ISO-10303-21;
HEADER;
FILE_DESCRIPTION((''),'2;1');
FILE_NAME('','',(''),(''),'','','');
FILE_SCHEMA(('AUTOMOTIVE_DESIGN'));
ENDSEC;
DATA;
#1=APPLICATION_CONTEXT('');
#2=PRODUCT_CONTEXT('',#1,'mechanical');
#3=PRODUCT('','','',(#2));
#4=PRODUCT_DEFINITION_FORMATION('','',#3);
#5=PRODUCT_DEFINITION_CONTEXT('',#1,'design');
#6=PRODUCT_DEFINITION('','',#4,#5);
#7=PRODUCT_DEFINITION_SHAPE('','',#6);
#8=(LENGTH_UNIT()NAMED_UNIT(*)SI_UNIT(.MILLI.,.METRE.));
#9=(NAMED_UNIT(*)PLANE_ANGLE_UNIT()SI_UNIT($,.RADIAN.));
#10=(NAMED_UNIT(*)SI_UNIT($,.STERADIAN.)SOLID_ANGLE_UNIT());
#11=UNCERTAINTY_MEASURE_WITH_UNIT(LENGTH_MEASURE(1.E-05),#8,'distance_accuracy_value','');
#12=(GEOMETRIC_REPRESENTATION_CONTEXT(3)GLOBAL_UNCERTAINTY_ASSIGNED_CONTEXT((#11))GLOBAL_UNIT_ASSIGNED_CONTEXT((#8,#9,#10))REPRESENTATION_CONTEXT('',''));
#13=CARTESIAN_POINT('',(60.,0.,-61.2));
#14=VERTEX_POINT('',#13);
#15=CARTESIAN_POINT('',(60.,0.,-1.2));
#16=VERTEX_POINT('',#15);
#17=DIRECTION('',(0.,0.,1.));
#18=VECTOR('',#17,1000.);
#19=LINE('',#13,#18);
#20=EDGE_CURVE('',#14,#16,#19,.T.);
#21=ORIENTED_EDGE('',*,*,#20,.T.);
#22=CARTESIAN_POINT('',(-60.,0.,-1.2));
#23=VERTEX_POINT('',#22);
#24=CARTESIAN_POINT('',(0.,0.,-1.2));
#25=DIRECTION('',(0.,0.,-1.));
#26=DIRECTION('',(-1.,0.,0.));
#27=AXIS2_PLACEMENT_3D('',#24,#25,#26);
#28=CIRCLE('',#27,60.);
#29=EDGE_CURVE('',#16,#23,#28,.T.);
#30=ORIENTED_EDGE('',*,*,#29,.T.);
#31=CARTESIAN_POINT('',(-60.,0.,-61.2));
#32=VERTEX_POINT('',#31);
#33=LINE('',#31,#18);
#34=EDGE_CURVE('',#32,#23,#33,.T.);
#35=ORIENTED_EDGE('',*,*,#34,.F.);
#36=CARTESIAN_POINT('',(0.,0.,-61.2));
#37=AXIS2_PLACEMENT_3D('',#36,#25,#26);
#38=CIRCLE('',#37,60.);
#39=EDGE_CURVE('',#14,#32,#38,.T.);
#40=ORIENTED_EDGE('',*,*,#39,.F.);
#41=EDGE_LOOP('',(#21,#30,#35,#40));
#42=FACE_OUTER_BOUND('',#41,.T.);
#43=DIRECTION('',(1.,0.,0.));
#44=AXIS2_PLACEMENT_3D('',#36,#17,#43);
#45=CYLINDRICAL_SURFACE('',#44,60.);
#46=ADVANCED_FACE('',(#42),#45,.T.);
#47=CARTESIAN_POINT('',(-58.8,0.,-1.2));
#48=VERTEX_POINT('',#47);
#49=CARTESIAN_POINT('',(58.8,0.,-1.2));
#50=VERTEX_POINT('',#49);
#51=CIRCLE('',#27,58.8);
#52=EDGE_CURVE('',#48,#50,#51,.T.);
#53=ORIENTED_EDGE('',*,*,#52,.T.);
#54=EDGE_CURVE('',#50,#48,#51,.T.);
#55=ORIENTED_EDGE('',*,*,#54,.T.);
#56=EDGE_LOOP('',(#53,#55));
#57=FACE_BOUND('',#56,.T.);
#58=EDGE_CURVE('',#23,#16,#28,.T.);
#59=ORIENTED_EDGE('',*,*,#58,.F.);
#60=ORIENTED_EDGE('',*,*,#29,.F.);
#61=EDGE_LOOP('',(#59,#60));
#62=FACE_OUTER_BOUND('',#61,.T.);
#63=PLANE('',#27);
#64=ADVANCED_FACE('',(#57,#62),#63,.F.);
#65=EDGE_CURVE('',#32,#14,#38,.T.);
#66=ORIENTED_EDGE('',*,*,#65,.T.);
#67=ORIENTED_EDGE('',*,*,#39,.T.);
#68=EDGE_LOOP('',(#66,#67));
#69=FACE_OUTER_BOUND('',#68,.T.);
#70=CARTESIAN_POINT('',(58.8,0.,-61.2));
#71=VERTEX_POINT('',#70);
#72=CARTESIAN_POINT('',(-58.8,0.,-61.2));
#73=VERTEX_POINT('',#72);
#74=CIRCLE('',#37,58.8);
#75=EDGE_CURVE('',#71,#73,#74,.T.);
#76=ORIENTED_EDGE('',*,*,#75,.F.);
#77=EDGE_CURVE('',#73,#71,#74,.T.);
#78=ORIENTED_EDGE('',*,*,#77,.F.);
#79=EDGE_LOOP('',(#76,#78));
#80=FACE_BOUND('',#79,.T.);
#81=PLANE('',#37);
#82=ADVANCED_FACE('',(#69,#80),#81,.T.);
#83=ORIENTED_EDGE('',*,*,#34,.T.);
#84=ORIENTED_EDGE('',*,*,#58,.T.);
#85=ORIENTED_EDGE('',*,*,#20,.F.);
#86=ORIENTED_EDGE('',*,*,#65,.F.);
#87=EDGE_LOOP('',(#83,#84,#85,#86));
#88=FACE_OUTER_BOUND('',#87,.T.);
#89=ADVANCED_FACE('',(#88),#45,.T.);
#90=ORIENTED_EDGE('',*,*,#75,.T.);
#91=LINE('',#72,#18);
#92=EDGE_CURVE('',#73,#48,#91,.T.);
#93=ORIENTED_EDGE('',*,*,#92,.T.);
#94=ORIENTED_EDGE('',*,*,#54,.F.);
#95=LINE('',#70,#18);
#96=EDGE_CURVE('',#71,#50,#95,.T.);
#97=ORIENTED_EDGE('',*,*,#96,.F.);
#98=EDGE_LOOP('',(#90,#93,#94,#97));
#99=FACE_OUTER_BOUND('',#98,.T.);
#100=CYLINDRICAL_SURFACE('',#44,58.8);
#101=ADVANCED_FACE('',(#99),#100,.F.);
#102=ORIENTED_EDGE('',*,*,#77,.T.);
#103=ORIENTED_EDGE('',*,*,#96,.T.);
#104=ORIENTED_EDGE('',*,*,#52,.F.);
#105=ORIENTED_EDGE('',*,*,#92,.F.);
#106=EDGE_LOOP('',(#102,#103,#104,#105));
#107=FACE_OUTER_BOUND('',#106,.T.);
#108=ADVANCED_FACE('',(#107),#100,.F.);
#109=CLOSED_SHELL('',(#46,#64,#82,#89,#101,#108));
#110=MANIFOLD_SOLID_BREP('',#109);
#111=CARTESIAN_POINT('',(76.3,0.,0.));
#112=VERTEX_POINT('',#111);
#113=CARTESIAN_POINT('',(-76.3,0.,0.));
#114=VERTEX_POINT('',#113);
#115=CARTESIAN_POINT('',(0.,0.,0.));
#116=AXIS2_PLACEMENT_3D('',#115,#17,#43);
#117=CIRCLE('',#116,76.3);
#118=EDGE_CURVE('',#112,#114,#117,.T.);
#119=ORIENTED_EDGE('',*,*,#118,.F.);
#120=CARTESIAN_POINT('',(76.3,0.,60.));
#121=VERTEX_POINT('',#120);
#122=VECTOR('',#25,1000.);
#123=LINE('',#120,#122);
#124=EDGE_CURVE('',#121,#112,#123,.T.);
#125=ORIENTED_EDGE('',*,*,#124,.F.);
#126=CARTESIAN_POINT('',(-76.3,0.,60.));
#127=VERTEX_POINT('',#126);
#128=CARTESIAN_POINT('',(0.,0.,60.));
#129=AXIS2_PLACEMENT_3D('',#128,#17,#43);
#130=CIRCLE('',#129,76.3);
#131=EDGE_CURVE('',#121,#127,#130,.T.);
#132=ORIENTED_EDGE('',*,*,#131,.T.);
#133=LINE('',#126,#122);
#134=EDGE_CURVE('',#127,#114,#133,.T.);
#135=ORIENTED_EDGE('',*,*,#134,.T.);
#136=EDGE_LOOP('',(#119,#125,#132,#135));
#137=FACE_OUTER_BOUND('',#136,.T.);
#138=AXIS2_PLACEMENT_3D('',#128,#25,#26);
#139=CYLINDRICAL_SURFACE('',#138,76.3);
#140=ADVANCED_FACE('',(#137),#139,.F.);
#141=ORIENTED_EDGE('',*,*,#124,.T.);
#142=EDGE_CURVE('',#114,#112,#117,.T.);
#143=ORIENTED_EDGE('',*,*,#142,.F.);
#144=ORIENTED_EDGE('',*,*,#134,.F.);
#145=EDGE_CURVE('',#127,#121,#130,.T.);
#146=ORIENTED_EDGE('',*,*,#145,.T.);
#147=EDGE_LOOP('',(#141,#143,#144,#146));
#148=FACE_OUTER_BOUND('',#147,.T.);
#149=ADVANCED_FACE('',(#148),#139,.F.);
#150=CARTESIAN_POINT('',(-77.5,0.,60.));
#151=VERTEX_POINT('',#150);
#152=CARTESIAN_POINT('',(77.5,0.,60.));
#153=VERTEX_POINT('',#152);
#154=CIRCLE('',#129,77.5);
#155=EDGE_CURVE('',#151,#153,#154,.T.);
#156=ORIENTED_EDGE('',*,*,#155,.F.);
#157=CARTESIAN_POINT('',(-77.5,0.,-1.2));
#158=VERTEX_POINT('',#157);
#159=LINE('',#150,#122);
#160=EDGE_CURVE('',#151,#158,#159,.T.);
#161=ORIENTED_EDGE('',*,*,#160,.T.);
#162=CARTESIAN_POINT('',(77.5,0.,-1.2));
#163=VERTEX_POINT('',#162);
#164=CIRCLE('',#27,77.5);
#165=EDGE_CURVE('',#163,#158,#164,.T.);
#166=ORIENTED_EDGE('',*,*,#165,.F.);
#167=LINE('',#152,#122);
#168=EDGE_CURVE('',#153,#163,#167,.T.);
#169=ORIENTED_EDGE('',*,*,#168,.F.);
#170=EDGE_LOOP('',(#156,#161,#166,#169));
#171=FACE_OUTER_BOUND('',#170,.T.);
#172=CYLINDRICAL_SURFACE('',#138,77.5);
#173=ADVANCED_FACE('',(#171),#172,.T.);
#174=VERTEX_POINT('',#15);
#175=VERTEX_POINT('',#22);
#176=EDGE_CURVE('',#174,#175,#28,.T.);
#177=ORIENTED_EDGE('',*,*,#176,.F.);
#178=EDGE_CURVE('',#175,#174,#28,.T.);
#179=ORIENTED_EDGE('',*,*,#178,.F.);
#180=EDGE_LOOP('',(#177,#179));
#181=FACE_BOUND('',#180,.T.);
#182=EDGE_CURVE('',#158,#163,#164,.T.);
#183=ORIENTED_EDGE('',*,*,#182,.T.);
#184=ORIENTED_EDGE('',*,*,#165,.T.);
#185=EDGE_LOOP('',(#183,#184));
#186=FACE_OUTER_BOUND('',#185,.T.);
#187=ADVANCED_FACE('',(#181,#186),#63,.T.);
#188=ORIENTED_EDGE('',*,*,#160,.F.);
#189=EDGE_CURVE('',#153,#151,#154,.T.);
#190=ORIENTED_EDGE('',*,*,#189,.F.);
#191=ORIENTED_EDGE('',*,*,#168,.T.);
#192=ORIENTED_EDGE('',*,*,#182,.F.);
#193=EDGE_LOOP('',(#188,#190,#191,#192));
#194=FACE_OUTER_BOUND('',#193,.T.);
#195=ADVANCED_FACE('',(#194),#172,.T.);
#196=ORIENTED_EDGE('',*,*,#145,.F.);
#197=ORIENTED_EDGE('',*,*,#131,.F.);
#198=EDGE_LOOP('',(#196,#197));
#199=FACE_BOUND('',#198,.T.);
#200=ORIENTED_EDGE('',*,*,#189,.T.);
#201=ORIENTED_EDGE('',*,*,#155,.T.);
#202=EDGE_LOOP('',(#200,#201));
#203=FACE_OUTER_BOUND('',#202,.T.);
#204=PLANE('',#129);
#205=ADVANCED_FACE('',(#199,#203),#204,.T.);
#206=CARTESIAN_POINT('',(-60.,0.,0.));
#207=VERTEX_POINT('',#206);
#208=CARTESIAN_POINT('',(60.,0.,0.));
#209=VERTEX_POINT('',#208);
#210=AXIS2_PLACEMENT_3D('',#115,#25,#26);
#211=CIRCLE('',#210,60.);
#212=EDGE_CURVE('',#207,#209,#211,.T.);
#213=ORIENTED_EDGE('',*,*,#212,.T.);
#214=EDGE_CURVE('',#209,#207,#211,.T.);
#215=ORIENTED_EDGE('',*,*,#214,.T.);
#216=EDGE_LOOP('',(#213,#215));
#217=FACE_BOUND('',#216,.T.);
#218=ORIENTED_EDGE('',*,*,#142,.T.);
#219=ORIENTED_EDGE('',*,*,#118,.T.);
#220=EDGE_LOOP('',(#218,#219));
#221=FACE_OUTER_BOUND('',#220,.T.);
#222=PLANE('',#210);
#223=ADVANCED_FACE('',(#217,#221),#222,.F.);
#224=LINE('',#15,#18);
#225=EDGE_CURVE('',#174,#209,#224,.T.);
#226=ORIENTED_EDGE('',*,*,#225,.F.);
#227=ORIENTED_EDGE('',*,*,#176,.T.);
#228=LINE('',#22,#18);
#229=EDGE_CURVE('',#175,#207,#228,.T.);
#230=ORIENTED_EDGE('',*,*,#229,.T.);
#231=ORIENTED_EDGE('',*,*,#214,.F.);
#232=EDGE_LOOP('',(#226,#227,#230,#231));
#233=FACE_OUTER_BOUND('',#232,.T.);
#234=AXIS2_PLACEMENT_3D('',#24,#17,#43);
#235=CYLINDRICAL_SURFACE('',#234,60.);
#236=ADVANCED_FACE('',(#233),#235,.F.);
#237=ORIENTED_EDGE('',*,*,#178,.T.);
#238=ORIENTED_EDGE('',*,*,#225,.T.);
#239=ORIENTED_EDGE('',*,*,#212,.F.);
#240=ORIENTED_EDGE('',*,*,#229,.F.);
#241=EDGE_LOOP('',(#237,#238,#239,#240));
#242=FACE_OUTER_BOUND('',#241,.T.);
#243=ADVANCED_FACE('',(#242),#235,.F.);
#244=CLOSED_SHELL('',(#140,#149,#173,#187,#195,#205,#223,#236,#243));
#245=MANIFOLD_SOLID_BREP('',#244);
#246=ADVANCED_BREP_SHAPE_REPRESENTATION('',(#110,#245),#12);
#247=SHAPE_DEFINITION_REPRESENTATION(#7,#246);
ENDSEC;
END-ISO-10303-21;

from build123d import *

# Parameters (mm, degrees)
SKETCH1_R           = 77.5
SKETCH1_R_2         = 76.3
BOSS_EXTRUDE1_DEPTH = 60
BOSS_EXTRUDE2_START = 1.2
SKETCH2_R           = 77.5
SKETCH2_R_2         = 60
BOSS_EXTRUDE2_DEPTH = 1.2
SKETCH3_R           = 60
SKETCH3_R_2         = 58.8
BOSS_EXTRUDE3_DEPTH = 60


with BuildPart() as part:
    # Sketch1 → Boss-Extrude1 (new body)
    with BuildSketch(Plane.XY):
        Circle(SKETCH1_R)
        Circle(SKETCH1_R_2, mode=Mode.SUBTRACT)
    extrude(amount=BOSS_EXTRUDE1_DEPTH)

    # Sketch2 → Boss-Extrude2 (add)
    with BuildSketch(Plane(origin=(0, 0, 0), x_dir=(-1, 0, 0), z_dir=(0, 0, -1)).offset(BOSS_EXTRUDE2_START)):
        Circle(SKETCH2_R)
        Circle(SKETCH2_R_2, mode=Mode.SUBTRACT)
    extrude(amount=-BOSS_EXTRUDE2_DEPTH)


with BuildPart() as body_2:
    # Sketch3 → Boss-Extrude3 (new body)
    with BuildSketch(Plane(origin=(0, 0, -1.2), x_dir=(-1, 0, 0), z_dir=(0, 0, -1))):
        Circle(SKETCH3_R)
        Circle(SKETCH3_R_2, mode=Mode.SUBTRACT)
    extrude(amount=BOSS_EXTRUDE3_DEPTH)


solid = Compound([part.part, body_2.part])
